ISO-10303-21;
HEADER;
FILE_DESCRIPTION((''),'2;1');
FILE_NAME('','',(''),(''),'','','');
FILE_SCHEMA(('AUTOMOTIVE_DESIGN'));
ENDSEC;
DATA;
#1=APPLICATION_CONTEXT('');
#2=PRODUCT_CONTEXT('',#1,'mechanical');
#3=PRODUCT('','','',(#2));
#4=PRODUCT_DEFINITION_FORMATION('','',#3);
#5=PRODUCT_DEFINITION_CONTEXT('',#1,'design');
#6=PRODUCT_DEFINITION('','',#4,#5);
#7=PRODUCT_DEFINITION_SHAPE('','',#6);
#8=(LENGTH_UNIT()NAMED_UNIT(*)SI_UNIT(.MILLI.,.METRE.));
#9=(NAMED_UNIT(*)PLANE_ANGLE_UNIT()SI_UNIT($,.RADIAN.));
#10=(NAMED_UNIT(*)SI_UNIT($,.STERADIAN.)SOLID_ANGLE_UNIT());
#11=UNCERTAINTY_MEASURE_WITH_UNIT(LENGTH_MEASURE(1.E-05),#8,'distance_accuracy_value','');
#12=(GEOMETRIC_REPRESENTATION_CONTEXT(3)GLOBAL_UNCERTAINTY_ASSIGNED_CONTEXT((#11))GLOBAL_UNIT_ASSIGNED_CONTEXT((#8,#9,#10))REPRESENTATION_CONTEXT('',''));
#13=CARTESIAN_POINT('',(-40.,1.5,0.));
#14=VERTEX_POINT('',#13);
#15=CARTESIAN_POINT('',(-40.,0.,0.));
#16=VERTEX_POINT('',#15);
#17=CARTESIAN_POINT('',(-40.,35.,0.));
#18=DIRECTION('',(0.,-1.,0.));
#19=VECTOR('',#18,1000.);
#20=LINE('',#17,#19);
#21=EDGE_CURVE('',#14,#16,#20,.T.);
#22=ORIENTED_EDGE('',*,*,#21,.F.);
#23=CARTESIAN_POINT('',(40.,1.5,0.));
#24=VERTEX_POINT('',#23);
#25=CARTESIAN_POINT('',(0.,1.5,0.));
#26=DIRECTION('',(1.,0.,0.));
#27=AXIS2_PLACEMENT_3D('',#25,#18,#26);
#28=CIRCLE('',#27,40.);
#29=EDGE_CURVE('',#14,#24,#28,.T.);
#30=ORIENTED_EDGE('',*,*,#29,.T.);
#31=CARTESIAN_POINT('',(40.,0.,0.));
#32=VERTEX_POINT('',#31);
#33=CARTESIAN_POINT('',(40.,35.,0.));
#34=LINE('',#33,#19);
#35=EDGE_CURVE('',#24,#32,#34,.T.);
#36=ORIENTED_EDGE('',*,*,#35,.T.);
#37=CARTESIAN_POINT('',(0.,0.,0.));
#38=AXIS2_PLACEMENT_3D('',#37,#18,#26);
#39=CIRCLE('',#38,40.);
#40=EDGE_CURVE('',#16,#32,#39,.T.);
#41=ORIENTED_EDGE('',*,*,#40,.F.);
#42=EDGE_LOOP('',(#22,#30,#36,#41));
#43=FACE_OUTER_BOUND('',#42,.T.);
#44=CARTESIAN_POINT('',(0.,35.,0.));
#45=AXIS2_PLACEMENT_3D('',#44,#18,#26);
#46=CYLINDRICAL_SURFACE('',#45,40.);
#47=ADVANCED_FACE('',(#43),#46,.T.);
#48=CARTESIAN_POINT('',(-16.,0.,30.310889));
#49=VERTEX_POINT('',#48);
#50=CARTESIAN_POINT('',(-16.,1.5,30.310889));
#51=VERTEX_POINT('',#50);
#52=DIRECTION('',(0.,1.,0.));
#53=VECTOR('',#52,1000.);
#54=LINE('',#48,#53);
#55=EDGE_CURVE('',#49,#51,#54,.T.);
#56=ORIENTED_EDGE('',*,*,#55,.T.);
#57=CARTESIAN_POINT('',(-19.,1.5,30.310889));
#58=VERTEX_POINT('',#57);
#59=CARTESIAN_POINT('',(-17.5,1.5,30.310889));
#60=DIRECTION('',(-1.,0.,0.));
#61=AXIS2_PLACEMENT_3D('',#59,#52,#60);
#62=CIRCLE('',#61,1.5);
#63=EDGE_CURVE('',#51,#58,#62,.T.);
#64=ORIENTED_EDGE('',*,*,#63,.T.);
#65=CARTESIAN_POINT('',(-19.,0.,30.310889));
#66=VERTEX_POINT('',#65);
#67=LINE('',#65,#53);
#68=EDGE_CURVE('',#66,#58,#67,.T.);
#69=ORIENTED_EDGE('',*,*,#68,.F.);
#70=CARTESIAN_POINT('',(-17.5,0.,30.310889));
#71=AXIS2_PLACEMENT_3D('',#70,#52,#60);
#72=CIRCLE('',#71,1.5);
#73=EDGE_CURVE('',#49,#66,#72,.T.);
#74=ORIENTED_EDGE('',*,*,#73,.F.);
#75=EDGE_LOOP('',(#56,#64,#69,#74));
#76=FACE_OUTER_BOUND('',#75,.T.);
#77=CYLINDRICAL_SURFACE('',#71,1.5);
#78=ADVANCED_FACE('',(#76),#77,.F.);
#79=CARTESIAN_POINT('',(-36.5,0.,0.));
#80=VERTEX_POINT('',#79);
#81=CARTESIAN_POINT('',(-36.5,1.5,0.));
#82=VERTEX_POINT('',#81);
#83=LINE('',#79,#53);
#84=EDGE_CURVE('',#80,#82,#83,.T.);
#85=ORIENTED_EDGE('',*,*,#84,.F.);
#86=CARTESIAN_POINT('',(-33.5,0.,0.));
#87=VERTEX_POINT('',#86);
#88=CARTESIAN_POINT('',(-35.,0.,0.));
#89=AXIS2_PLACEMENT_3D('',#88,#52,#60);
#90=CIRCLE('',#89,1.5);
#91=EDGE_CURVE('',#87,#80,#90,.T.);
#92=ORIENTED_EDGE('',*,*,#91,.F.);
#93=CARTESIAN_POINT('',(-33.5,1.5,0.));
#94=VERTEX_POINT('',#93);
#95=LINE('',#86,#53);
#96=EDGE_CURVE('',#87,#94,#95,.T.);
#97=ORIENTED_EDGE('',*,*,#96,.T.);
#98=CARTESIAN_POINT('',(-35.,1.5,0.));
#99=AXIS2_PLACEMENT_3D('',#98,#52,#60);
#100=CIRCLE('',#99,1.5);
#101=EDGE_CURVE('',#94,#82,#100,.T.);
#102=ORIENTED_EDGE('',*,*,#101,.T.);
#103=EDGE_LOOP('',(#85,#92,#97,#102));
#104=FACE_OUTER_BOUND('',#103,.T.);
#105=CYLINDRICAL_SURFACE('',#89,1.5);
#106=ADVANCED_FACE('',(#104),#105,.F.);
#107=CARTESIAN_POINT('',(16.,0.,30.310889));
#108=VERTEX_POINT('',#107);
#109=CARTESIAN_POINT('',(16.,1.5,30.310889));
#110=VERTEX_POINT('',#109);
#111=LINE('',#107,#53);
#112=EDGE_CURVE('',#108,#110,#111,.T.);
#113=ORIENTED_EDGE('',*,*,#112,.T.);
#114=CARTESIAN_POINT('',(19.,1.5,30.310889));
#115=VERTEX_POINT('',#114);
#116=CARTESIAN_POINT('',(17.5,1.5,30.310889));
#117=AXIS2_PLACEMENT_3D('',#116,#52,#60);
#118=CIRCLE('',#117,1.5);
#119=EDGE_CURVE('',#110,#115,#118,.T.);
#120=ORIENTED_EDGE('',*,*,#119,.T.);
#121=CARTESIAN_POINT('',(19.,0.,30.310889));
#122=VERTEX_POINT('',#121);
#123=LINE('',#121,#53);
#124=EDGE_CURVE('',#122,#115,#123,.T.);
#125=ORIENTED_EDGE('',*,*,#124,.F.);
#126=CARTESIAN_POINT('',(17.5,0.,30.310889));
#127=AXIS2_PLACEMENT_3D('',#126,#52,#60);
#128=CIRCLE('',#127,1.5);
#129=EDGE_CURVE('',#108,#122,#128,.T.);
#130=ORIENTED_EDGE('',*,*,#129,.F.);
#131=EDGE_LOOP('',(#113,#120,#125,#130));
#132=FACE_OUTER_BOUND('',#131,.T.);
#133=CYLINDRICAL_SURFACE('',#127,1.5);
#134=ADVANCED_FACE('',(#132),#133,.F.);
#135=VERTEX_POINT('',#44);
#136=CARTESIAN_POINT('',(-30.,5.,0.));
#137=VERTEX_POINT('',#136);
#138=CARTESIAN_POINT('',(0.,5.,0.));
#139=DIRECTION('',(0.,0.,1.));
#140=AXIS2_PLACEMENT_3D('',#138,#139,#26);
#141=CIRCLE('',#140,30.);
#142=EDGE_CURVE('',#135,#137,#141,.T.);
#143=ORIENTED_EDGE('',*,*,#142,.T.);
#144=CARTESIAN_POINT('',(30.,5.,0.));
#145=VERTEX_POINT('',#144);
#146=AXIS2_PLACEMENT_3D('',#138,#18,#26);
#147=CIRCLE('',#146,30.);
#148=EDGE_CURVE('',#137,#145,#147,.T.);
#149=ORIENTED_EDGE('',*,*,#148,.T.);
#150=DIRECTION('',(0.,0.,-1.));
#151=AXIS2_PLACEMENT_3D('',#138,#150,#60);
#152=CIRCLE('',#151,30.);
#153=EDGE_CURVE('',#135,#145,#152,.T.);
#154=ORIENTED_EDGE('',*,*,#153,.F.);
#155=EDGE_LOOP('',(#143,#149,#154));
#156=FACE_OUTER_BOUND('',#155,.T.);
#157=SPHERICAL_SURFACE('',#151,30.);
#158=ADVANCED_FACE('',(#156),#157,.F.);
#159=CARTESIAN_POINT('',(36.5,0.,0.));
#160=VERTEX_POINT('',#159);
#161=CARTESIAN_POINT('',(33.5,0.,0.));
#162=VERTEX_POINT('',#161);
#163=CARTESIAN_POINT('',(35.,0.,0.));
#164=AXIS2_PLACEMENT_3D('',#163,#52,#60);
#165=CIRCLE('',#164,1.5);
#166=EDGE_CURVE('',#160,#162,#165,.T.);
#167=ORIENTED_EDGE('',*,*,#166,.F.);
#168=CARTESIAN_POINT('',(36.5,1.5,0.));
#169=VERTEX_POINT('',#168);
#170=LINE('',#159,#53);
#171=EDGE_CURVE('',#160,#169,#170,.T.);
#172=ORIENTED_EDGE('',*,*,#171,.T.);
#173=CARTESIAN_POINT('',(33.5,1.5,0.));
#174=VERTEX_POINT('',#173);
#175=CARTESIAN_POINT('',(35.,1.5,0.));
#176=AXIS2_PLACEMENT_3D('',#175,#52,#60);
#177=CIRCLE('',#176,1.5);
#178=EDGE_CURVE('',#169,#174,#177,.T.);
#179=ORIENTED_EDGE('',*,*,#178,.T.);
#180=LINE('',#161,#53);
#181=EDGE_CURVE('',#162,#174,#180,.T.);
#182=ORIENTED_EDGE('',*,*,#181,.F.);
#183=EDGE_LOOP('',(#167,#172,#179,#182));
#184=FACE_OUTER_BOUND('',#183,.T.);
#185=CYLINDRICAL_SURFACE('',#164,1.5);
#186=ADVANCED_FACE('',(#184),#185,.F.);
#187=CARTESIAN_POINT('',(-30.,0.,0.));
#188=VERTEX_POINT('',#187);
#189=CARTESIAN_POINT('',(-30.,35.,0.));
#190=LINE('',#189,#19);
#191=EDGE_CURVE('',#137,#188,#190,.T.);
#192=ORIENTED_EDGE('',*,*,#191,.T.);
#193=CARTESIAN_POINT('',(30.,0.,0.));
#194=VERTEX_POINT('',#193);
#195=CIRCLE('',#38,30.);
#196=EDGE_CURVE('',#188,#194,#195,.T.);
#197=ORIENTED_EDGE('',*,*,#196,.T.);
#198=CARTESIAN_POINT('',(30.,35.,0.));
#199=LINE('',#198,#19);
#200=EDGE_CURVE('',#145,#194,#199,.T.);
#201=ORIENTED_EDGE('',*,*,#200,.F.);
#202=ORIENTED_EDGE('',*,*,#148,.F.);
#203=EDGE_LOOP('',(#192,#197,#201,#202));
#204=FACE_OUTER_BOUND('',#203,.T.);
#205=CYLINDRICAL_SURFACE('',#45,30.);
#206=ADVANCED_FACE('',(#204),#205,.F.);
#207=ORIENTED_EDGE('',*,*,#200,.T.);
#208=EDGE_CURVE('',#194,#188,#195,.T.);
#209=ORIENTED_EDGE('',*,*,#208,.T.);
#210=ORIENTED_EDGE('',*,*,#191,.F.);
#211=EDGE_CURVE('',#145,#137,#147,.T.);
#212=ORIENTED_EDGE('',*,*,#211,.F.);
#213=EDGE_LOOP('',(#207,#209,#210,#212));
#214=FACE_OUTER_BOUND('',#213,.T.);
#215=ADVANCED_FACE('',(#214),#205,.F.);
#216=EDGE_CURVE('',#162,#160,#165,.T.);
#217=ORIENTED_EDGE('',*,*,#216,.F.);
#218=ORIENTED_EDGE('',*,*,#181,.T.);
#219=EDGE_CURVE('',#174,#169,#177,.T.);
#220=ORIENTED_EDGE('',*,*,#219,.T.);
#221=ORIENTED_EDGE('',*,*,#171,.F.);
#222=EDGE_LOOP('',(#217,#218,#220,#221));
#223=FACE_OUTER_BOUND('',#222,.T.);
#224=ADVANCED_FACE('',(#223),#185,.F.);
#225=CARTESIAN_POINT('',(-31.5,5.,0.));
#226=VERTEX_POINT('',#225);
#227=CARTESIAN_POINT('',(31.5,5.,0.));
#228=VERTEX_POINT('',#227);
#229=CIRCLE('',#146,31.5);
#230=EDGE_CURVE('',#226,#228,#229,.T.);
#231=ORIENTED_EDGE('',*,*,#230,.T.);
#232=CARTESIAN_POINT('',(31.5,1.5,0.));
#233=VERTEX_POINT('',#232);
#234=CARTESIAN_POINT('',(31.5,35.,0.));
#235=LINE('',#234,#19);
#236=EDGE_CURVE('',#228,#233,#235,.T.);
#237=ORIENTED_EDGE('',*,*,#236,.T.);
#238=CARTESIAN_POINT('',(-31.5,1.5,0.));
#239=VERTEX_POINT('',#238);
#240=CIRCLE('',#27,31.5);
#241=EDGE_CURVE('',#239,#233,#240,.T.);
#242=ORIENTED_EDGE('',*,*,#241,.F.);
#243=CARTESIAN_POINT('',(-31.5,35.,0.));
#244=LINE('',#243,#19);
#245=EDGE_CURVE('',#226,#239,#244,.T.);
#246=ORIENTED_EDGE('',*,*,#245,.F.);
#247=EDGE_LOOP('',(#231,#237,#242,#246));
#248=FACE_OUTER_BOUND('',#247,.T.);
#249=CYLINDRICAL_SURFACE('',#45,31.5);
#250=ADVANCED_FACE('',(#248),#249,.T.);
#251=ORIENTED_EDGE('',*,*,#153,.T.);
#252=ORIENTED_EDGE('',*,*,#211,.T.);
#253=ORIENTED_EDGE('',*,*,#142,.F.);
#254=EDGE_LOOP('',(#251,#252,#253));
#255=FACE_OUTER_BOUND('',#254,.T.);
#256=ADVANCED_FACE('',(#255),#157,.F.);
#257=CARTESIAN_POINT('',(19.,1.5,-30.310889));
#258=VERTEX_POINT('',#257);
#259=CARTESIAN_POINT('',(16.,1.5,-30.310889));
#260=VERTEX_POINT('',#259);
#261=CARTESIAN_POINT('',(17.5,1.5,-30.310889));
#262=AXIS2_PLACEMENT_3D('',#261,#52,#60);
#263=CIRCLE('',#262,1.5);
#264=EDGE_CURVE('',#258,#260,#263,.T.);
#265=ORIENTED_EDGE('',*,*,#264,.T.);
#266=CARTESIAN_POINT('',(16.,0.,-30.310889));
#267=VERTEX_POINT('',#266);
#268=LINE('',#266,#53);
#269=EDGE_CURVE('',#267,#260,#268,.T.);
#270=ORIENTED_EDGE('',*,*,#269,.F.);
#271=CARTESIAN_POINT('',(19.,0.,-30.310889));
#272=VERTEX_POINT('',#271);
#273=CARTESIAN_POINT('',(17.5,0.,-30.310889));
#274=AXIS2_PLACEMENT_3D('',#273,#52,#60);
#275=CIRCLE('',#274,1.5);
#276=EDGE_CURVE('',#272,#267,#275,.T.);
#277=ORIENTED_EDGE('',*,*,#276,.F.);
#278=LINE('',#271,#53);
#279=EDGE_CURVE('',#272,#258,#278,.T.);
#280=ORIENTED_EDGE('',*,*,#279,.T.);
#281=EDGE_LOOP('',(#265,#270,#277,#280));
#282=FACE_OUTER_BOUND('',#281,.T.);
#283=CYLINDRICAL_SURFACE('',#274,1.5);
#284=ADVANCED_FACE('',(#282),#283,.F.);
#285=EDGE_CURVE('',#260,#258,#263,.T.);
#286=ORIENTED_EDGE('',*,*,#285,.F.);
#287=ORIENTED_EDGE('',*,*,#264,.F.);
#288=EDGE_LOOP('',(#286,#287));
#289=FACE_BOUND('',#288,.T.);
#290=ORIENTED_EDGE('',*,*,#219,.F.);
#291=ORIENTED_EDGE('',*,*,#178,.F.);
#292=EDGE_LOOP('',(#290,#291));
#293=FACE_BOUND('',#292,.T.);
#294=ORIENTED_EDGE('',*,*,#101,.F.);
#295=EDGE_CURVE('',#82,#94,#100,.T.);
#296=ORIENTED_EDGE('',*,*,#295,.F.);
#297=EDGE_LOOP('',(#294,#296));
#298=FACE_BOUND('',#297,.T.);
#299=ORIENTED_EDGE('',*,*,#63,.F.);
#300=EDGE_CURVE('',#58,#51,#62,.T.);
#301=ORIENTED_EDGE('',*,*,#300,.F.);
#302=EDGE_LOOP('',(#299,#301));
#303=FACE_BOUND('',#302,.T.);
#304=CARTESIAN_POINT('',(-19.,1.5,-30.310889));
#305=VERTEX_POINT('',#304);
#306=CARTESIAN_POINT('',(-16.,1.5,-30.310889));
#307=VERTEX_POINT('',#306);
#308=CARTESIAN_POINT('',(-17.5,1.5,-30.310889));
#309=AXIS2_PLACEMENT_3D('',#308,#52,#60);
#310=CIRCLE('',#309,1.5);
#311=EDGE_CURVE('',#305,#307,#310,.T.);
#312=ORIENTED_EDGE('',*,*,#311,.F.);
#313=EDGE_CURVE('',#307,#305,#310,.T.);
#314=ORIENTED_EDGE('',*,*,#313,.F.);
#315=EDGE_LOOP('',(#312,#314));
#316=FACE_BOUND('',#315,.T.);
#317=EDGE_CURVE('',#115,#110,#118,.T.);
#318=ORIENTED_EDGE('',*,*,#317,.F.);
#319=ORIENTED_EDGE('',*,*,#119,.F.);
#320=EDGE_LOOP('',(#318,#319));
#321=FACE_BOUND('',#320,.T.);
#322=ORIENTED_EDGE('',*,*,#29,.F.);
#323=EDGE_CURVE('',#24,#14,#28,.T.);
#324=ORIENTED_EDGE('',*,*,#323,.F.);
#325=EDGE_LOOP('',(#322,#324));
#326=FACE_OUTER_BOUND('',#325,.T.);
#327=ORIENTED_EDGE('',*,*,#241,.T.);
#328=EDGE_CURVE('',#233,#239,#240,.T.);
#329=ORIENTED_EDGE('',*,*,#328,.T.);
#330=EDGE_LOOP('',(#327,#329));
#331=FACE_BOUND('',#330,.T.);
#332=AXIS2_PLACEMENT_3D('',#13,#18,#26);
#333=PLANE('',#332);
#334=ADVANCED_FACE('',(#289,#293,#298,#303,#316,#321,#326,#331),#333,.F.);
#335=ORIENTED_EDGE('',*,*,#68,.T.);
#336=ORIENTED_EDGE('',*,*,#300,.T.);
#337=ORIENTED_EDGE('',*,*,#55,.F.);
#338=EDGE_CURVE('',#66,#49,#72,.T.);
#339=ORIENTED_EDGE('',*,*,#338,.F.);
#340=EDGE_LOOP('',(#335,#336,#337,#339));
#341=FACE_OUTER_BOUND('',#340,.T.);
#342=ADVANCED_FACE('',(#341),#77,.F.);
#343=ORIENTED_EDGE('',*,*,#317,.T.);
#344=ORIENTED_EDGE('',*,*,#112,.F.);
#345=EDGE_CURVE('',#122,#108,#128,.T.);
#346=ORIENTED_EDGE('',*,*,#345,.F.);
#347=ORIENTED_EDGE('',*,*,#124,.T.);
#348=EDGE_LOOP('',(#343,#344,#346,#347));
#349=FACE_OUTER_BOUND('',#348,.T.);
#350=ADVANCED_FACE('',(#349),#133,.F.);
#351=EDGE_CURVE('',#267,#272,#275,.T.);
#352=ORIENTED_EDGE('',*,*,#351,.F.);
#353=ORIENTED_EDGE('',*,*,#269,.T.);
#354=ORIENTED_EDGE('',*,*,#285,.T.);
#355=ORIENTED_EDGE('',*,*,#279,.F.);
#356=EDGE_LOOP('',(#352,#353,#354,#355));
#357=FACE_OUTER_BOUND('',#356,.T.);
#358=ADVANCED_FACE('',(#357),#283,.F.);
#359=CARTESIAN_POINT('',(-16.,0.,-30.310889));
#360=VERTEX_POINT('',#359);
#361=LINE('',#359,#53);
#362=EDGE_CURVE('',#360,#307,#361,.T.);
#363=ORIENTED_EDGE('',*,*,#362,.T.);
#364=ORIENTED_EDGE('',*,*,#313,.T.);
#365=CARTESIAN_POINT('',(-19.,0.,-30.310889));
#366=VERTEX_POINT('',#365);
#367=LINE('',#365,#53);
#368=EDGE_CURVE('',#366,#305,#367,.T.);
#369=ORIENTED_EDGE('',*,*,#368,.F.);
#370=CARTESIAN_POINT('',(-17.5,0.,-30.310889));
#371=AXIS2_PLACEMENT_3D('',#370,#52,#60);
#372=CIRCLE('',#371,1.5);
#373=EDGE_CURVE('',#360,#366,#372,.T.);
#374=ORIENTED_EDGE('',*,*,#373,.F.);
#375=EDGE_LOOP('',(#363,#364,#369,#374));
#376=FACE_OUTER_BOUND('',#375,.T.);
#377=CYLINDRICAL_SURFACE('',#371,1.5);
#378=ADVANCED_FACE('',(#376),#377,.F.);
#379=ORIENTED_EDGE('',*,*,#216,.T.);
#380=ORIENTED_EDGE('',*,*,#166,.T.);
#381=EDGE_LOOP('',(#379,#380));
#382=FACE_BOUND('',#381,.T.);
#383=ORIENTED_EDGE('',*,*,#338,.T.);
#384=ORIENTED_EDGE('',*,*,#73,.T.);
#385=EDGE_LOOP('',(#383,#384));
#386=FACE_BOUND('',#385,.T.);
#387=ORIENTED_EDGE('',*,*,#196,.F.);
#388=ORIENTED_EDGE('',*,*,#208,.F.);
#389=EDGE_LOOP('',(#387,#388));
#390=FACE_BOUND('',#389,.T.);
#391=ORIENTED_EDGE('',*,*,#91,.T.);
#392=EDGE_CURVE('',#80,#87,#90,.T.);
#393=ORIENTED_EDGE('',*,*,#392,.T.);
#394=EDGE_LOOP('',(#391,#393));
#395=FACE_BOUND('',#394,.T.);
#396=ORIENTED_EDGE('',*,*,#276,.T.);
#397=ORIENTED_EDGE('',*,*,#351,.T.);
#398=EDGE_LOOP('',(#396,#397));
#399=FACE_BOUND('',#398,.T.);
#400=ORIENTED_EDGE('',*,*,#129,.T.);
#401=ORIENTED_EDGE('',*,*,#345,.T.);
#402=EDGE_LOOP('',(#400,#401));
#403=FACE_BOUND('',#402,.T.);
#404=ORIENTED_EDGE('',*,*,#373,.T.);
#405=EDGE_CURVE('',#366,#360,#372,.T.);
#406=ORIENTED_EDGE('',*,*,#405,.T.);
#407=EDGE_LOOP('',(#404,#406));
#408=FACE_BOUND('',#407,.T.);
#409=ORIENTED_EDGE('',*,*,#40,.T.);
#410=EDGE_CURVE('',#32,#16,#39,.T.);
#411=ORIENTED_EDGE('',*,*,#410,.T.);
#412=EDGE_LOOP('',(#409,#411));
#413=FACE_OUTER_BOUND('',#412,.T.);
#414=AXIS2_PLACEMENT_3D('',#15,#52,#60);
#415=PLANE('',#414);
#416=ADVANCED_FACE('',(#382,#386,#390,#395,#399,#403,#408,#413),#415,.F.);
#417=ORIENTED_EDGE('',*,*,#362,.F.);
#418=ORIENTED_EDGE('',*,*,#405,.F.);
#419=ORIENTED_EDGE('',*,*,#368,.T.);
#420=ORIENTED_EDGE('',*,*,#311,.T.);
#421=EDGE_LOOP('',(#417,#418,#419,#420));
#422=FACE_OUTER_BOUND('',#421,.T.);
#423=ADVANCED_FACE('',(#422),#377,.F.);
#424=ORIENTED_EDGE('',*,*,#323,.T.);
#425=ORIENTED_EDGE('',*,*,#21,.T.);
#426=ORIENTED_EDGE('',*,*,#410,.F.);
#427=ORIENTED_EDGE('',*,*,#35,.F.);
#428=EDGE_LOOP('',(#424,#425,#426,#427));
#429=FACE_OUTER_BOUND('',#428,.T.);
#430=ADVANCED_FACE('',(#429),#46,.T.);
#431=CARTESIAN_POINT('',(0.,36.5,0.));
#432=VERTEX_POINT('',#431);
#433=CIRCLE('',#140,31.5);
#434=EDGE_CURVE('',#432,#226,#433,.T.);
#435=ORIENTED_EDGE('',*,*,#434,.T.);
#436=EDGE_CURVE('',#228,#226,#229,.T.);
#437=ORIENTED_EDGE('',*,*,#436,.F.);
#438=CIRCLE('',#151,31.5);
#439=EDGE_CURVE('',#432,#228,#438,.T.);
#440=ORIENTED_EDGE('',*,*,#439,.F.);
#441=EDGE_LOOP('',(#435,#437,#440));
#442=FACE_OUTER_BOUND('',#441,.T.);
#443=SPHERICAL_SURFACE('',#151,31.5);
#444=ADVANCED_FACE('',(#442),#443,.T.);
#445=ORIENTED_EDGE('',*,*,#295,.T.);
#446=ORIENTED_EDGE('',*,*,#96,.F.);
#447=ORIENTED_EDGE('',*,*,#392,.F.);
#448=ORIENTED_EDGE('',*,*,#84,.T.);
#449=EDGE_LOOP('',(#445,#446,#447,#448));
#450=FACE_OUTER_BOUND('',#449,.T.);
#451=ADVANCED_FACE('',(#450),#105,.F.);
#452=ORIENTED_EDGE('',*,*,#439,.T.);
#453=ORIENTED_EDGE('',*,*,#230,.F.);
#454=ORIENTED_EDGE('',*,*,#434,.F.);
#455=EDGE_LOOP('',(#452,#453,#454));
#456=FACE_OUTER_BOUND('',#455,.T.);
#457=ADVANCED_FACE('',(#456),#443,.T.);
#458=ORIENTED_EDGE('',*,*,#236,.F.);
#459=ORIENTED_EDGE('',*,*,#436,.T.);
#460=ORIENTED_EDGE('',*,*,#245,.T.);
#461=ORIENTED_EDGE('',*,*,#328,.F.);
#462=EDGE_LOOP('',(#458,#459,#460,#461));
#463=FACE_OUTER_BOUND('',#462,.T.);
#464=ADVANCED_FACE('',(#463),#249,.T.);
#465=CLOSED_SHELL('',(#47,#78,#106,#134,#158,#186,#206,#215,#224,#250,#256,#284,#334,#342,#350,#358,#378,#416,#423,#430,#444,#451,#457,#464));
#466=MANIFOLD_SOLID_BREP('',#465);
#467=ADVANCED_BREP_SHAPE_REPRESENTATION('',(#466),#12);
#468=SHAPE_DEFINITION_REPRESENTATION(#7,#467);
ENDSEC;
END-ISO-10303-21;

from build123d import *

# Parameters (mm, degrees)
SKETCH2_R          = 1.5
CUT_EXTRUDE1_DEPTH = 67.520673478


with BuildPart() as part:
    # Sketch1 → Revolve1 (revolve)
    with BuildSketch(Plane.XY, mode=Mode.PRIVATE) as revolve1_sk:
        with BuildLine():
            Line((-40, 0), (-30, 0))
            Line((-30, 0), (-30, 5))
            ThreePointArc((-30, 5), (-21.213203436, 26.213203436), (0, 35))
            Line((0, 35), (0, 36.5))
            ThreePointArc((0, 36.5), (-22.273863607, 27.273863607), (-31.5, 5))
            Line((-31.5, 5), (-31.5, 1.5))
            Line((-31.5, 1.5), (-40, 1.5))
            Line((-40, 1.5), (-40, 0))
        make_face()
    revolve(revolve1_sk.sketch.rotate(Axis((0, 35, 0), (0, 1, 0)), 180), axis=Axis((0, 35, 0), (0, 1, 0)))

    # Sketch2 → Cut-Extrude1 (cut, through all)
    with BuildSketch(Plane(origin=(0, 1.5, 0), x_dir=(1, 0, 0), z_dir=(0, 1, 0))):
        with Locations(Location((-35, 0, 0), (0, 0, 180))):
            Circle(SKETCH2_R)
        with Locations(Location((-17.5, 30.310889132, 0), (0, 0, 180))):
            Circle(SKETCH2_R)
        with Locations(Location((17.5, 30.310889132, 0), (0, 0, 180))):
            Circle(SKETCH2_R)
        with Locations(Location((35, 0, 0), (0, 0, 180))):
            Circle(SKETCH2_R)
        with Locations(Location((17.5, -30.310889132, 0), (0, 0, 180))):
            Circle(SKETCH2_R)
        with Locations(Location((-17.5, -30.310889132, 0), (0, 0, 180))):
            Circle(SKETCH2_R)
    extrude(amount=-CUT_EXTRUDE1_DEPTH, mode=Mode.SUBTRACT)


solid = part.part
